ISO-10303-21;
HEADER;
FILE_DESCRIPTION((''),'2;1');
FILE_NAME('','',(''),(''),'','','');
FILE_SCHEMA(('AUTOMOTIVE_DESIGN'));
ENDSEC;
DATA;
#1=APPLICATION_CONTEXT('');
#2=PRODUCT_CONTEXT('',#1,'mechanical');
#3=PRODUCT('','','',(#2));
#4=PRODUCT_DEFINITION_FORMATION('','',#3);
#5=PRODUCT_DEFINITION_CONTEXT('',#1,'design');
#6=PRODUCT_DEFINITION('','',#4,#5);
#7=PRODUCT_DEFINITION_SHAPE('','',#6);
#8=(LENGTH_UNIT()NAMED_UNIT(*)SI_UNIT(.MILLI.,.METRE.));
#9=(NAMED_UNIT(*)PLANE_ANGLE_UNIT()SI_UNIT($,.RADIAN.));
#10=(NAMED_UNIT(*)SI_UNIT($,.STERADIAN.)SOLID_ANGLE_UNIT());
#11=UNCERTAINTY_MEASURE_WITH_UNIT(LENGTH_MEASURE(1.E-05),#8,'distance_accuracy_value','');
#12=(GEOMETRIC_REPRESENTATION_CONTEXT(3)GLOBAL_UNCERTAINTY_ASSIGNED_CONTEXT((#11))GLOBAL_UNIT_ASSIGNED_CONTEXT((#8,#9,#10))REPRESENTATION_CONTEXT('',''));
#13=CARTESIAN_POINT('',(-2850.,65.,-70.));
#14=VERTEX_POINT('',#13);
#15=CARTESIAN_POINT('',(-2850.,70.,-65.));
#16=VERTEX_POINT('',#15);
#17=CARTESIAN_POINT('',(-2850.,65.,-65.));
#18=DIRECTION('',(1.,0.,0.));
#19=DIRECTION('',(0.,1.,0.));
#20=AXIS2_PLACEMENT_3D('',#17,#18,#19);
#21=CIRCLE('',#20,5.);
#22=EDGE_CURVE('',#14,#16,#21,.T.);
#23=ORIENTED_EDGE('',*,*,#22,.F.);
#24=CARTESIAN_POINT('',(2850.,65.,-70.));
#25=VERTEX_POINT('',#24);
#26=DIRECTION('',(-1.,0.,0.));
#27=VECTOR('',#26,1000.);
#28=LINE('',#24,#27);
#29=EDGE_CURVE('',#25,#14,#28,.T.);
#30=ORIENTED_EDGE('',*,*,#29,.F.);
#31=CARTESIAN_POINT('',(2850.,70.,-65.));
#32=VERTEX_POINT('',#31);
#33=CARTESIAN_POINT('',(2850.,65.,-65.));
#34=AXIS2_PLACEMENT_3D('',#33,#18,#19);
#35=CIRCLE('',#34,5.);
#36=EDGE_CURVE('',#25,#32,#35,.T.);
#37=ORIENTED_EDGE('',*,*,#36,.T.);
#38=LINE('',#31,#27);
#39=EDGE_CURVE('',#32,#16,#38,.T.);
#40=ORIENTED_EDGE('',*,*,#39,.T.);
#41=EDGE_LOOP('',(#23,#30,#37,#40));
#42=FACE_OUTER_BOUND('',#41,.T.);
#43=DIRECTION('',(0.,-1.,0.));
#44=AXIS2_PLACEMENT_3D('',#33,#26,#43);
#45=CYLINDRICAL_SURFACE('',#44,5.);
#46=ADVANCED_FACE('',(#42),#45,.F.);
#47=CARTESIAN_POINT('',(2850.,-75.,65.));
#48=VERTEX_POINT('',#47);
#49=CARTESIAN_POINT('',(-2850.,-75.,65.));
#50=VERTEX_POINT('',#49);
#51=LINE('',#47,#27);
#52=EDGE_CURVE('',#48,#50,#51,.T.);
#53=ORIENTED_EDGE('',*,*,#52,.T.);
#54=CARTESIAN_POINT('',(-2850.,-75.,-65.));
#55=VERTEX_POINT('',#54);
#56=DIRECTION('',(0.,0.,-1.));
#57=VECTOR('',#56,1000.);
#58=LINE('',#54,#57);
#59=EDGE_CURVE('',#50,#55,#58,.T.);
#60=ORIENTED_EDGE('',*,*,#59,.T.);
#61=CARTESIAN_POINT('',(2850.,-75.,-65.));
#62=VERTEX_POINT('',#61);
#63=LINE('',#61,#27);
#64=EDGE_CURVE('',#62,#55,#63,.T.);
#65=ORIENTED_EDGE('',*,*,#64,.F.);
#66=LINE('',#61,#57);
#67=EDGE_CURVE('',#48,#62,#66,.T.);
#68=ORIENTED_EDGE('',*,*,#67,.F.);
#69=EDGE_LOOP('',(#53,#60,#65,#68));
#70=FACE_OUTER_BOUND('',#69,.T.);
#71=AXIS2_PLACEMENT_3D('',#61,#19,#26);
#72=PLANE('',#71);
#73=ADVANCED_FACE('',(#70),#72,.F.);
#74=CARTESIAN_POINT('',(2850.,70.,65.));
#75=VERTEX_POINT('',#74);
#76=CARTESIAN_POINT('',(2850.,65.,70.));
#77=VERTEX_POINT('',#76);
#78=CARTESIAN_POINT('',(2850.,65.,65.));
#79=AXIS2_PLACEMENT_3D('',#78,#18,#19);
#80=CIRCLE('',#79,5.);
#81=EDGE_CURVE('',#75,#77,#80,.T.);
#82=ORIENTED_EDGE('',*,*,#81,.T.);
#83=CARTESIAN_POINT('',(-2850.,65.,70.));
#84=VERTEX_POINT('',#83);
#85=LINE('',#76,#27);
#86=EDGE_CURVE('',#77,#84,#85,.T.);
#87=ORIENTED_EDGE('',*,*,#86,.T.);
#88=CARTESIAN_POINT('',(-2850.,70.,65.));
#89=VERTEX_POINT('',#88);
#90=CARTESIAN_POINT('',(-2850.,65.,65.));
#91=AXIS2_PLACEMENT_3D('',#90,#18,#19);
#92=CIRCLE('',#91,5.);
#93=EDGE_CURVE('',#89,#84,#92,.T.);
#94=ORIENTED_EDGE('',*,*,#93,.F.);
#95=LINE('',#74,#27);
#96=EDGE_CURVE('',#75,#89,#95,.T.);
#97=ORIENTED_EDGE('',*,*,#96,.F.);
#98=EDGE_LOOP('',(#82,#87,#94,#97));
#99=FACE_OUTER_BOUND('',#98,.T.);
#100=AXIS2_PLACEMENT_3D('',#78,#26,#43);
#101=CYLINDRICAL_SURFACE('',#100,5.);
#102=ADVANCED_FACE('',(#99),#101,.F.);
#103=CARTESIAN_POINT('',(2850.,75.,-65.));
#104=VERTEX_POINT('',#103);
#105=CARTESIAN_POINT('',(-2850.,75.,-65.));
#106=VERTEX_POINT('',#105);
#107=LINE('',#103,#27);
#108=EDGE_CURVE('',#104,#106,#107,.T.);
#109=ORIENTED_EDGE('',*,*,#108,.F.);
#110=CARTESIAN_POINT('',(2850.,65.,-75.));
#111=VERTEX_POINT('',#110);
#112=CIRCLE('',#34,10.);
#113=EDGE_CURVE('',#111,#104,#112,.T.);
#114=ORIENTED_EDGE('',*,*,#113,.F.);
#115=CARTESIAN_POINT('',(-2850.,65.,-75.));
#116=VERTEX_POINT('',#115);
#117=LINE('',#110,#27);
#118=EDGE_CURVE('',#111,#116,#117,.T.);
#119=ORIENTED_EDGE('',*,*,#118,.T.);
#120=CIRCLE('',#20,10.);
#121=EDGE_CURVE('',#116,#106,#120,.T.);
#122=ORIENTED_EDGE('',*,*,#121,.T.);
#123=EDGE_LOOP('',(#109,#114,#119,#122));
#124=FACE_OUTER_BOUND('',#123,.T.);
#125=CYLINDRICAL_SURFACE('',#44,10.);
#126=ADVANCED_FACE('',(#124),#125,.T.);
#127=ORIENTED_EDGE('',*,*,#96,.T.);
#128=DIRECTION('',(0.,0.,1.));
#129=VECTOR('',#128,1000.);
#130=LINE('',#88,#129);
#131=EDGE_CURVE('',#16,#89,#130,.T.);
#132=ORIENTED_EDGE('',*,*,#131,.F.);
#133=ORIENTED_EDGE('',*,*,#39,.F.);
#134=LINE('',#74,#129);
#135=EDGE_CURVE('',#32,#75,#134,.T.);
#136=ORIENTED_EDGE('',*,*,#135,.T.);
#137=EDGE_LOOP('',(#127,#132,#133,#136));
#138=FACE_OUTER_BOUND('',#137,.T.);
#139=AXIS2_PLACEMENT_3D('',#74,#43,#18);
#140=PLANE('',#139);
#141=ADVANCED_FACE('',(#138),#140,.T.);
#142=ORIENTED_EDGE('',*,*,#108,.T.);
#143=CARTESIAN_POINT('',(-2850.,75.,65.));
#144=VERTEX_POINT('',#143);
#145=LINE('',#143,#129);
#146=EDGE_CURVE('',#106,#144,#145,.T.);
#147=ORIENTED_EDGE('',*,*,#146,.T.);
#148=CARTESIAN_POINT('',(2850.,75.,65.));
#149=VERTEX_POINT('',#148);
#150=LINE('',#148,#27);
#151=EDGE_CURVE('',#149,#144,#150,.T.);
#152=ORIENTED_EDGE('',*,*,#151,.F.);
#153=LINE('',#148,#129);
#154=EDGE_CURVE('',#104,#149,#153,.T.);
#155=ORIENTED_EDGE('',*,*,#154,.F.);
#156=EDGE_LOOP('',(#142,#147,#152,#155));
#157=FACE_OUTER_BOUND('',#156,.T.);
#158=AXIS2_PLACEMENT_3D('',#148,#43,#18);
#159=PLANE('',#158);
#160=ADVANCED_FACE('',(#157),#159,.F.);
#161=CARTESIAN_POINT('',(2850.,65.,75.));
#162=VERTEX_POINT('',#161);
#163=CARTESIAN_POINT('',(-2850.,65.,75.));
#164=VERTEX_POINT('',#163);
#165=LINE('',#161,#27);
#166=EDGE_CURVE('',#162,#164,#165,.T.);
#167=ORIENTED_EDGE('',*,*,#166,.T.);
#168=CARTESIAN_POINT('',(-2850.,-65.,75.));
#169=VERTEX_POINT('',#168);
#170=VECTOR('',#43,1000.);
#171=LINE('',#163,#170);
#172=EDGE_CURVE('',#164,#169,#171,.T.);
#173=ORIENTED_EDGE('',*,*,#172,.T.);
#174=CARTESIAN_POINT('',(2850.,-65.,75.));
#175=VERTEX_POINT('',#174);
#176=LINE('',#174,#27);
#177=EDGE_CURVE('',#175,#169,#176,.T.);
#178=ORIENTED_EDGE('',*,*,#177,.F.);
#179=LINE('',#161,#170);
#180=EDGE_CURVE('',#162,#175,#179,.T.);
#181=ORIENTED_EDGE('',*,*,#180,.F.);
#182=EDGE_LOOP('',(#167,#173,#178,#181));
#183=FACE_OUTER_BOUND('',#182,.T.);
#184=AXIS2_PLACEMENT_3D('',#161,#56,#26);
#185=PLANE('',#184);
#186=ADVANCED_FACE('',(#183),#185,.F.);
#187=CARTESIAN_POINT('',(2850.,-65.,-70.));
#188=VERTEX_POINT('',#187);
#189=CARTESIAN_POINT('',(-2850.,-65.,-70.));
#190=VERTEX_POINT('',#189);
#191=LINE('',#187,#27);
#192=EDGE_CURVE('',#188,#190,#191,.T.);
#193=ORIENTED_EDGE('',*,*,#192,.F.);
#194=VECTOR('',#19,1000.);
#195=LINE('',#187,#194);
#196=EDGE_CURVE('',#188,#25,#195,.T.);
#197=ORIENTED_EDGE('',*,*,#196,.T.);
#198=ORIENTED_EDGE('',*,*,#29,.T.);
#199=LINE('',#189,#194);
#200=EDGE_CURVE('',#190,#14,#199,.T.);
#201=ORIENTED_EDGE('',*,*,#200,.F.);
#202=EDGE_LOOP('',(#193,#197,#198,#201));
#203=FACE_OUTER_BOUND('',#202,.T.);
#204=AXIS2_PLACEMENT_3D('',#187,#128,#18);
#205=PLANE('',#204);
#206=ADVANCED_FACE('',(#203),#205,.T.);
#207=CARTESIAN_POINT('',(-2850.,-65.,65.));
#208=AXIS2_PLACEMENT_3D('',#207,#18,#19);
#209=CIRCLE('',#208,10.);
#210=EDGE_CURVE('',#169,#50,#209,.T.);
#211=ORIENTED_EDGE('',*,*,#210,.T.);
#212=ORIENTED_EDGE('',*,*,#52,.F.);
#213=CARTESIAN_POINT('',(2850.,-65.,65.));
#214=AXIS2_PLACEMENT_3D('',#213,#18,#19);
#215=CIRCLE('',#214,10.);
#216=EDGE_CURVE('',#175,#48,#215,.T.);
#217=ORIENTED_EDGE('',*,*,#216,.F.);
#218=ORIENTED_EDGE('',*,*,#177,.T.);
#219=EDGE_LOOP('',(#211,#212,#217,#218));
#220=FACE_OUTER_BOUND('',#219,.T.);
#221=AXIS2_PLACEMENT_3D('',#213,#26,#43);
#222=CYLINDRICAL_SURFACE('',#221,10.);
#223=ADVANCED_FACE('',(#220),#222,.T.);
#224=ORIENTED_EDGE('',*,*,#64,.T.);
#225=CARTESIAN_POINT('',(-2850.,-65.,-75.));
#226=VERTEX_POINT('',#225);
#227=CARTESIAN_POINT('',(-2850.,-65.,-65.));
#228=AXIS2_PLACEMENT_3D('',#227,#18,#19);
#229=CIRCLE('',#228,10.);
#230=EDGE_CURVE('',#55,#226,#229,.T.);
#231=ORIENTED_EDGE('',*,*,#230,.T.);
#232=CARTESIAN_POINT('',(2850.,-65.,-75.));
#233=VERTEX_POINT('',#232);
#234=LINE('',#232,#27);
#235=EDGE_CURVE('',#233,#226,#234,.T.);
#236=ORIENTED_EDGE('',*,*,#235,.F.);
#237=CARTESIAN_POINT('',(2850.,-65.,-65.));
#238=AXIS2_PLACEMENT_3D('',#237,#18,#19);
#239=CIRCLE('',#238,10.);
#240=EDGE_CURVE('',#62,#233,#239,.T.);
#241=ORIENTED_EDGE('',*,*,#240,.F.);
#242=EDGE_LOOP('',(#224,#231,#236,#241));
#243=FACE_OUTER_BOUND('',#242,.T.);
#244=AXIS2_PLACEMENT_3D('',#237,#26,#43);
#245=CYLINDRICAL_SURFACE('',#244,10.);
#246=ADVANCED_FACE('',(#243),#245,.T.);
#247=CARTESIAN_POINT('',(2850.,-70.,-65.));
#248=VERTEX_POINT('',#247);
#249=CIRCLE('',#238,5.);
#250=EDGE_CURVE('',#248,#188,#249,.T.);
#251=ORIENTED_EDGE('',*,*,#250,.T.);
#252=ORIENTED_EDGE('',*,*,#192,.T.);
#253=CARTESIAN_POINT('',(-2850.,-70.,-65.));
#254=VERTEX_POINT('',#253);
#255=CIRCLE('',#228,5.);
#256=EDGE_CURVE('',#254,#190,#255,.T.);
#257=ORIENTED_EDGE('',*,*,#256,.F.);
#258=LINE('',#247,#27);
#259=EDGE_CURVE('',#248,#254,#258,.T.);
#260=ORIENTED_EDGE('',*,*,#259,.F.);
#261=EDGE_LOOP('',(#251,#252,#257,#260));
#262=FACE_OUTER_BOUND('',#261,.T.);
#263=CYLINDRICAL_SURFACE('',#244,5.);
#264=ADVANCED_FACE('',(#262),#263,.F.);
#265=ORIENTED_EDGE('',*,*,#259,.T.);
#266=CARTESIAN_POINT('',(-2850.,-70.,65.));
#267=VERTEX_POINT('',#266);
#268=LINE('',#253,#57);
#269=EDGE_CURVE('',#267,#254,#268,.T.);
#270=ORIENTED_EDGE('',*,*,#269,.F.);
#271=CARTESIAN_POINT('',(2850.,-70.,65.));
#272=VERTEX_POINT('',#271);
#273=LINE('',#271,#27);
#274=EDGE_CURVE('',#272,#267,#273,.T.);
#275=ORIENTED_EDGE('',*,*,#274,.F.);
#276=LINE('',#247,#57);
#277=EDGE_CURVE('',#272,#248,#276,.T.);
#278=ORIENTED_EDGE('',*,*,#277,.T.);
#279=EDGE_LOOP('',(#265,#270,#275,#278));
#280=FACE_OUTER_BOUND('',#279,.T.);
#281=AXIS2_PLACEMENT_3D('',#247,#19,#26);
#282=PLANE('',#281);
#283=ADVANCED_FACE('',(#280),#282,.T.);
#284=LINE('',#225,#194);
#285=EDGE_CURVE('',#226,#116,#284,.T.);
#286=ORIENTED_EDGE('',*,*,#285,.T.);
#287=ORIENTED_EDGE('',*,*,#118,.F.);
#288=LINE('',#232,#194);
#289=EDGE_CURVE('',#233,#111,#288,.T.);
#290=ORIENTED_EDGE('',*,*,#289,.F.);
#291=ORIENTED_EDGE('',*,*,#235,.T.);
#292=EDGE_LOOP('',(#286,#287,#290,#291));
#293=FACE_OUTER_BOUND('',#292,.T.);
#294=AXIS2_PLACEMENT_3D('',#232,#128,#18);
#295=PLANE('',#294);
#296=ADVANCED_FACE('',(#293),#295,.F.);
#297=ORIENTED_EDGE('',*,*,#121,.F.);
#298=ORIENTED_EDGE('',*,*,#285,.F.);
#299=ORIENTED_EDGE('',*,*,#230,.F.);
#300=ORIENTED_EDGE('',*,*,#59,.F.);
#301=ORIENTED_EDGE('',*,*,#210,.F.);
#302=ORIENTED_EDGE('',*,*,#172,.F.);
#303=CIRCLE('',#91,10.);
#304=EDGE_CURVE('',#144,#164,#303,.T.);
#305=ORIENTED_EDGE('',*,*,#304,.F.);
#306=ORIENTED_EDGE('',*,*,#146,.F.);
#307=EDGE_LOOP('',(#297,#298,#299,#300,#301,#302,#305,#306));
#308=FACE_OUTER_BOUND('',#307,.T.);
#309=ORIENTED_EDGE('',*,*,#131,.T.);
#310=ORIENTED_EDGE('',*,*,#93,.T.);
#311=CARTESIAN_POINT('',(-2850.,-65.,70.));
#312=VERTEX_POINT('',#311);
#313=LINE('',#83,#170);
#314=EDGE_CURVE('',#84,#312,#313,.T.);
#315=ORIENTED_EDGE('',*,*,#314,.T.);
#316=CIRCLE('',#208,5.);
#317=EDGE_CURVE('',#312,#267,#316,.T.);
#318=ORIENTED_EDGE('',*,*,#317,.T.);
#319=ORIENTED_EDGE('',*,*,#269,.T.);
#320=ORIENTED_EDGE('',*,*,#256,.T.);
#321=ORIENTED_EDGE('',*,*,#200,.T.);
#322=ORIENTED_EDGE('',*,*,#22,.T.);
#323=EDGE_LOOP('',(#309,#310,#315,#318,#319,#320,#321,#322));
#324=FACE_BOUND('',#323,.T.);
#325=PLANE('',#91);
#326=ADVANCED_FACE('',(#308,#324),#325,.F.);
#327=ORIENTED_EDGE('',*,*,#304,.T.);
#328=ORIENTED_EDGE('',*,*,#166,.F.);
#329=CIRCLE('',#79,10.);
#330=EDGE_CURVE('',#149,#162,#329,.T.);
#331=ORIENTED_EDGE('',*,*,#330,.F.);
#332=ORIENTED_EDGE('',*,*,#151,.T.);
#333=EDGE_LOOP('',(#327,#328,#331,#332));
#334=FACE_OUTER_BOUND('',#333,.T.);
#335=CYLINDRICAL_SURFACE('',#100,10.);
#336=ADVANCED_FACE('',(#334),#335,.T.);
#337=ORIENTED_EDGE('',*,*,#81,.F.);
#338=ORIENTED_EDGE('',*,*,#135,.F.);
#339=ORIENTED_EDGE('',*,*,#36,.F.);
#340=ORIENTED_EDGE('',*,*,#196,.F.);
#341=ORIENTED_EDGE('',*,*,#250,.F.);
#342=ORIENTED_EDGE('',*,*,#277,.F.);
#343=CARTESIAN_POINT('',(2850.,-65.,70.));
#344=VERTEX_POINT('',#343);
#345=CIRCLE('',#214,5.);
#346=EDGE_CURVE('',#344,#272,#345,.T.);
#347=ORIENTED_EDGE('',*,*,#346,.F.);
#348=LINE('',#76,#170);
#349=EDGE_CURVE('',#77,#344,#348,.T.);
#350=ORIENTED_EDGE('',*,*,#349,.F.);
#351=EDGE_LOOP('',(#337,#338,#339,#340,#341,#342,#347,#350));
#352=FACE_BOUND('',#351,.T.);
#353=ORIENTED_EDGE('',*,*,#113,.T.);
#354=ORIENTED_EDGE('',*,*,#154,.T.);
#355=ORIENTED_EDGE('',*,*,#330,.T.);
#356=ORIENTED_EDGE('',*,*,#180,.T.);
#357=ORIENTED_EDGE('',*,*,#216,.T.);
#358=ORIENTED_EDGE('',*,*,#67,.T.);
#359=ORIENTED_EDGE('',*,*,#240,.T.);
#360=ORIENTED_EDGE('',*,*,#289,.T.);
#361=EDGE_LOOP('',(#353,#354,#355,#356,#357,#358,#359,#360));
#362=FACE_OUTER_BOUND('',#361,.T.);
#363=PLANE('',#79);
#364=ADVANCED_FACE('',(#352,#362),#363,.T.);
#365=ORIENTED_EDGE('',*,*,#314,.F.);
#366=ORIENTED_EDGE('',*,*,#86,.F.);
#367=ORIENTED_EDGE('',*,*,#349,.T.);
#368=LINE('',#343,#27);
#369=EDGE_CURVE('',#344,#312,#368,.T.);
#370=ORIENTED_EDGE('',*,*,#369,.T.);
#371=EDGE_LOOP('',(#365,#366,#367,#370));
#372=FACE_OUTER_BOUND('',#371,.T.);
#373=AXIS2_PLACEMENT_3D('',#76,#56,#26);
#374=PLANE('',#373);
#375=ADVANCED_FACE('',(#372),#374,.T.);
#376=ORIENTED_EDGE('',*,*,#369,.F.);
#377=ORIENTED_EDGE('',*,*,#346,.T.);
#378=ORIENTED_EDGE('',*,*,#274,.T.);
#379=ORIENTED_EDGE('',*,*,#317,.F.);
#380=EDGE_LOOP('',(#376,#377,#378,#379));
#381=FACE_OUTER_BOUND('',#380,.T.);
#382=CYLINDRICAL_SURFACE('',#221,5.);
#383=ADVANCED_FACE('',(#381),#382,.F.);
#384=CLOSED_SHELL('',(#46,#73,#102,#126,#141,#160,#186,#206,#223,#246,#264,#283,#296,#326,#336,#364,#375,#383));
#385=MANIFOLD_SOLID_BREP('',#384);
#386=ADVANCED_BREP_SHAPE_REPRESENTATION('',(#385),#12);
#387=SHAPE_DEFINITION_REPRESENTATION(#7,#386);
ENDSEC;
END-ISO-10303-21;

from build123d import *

# Parameters (mm, degrees)
GB_6728_1986_150_X_150_X_5_1_DEPTH = 5700


with BuildPart() as part:
    # Sketch1 → Gb／6728-1986方形空心型钢 150 X 150 X 5(1) (new body)
    with BuildSketch(Plane.YZ.offset(-2850)):
        with BuildLine():
            Line((-65, -75), (65, -75))
            ThreePointArc((65, -75), (72.071067812, -72.071067812), (75, -65))
            Line((75, -65), (75, 65))
            ThreePointArc((75, 65), (72.071067812, 72.071067812), (65, 75))
            Line((65, 75), (-65, 75))
            ThreePointArc((-65, 75), (-72.071067812, 72.071067812), (-75, 65))
            Line((-75, 65), (-75, -65))
            ThreePointArc((-75, -65), (-72.071067812, -72.071067812), (-65, -75))
        make_face()
        with BuildLine():
            Line((-65, -70), (65, -70))
            ThreePointArc((65, -70), (68.535533906, -68.535533906), (70, -65))
            Line((70, -65), (70, 65))
            ThreePointArc((70, 65), (68.535533906, 68.535533906), (65, 70))
            Line((65, 70), (-65, 70))
            ThreePointArc((-65, 70), (-68.535533906, 68.535533906), (-70, 65))
            Line((-70, 65), (-70, -65))
            ThreePointArc((-70, -65), (-68.535533906, -68.535533906), (-65, -70))
        make_face(mode=Mode.SUBTRACT)
    extrude(amount=GB_6728_1986_150_X_150_X_5_1_DEPTH)


solid = part.part
